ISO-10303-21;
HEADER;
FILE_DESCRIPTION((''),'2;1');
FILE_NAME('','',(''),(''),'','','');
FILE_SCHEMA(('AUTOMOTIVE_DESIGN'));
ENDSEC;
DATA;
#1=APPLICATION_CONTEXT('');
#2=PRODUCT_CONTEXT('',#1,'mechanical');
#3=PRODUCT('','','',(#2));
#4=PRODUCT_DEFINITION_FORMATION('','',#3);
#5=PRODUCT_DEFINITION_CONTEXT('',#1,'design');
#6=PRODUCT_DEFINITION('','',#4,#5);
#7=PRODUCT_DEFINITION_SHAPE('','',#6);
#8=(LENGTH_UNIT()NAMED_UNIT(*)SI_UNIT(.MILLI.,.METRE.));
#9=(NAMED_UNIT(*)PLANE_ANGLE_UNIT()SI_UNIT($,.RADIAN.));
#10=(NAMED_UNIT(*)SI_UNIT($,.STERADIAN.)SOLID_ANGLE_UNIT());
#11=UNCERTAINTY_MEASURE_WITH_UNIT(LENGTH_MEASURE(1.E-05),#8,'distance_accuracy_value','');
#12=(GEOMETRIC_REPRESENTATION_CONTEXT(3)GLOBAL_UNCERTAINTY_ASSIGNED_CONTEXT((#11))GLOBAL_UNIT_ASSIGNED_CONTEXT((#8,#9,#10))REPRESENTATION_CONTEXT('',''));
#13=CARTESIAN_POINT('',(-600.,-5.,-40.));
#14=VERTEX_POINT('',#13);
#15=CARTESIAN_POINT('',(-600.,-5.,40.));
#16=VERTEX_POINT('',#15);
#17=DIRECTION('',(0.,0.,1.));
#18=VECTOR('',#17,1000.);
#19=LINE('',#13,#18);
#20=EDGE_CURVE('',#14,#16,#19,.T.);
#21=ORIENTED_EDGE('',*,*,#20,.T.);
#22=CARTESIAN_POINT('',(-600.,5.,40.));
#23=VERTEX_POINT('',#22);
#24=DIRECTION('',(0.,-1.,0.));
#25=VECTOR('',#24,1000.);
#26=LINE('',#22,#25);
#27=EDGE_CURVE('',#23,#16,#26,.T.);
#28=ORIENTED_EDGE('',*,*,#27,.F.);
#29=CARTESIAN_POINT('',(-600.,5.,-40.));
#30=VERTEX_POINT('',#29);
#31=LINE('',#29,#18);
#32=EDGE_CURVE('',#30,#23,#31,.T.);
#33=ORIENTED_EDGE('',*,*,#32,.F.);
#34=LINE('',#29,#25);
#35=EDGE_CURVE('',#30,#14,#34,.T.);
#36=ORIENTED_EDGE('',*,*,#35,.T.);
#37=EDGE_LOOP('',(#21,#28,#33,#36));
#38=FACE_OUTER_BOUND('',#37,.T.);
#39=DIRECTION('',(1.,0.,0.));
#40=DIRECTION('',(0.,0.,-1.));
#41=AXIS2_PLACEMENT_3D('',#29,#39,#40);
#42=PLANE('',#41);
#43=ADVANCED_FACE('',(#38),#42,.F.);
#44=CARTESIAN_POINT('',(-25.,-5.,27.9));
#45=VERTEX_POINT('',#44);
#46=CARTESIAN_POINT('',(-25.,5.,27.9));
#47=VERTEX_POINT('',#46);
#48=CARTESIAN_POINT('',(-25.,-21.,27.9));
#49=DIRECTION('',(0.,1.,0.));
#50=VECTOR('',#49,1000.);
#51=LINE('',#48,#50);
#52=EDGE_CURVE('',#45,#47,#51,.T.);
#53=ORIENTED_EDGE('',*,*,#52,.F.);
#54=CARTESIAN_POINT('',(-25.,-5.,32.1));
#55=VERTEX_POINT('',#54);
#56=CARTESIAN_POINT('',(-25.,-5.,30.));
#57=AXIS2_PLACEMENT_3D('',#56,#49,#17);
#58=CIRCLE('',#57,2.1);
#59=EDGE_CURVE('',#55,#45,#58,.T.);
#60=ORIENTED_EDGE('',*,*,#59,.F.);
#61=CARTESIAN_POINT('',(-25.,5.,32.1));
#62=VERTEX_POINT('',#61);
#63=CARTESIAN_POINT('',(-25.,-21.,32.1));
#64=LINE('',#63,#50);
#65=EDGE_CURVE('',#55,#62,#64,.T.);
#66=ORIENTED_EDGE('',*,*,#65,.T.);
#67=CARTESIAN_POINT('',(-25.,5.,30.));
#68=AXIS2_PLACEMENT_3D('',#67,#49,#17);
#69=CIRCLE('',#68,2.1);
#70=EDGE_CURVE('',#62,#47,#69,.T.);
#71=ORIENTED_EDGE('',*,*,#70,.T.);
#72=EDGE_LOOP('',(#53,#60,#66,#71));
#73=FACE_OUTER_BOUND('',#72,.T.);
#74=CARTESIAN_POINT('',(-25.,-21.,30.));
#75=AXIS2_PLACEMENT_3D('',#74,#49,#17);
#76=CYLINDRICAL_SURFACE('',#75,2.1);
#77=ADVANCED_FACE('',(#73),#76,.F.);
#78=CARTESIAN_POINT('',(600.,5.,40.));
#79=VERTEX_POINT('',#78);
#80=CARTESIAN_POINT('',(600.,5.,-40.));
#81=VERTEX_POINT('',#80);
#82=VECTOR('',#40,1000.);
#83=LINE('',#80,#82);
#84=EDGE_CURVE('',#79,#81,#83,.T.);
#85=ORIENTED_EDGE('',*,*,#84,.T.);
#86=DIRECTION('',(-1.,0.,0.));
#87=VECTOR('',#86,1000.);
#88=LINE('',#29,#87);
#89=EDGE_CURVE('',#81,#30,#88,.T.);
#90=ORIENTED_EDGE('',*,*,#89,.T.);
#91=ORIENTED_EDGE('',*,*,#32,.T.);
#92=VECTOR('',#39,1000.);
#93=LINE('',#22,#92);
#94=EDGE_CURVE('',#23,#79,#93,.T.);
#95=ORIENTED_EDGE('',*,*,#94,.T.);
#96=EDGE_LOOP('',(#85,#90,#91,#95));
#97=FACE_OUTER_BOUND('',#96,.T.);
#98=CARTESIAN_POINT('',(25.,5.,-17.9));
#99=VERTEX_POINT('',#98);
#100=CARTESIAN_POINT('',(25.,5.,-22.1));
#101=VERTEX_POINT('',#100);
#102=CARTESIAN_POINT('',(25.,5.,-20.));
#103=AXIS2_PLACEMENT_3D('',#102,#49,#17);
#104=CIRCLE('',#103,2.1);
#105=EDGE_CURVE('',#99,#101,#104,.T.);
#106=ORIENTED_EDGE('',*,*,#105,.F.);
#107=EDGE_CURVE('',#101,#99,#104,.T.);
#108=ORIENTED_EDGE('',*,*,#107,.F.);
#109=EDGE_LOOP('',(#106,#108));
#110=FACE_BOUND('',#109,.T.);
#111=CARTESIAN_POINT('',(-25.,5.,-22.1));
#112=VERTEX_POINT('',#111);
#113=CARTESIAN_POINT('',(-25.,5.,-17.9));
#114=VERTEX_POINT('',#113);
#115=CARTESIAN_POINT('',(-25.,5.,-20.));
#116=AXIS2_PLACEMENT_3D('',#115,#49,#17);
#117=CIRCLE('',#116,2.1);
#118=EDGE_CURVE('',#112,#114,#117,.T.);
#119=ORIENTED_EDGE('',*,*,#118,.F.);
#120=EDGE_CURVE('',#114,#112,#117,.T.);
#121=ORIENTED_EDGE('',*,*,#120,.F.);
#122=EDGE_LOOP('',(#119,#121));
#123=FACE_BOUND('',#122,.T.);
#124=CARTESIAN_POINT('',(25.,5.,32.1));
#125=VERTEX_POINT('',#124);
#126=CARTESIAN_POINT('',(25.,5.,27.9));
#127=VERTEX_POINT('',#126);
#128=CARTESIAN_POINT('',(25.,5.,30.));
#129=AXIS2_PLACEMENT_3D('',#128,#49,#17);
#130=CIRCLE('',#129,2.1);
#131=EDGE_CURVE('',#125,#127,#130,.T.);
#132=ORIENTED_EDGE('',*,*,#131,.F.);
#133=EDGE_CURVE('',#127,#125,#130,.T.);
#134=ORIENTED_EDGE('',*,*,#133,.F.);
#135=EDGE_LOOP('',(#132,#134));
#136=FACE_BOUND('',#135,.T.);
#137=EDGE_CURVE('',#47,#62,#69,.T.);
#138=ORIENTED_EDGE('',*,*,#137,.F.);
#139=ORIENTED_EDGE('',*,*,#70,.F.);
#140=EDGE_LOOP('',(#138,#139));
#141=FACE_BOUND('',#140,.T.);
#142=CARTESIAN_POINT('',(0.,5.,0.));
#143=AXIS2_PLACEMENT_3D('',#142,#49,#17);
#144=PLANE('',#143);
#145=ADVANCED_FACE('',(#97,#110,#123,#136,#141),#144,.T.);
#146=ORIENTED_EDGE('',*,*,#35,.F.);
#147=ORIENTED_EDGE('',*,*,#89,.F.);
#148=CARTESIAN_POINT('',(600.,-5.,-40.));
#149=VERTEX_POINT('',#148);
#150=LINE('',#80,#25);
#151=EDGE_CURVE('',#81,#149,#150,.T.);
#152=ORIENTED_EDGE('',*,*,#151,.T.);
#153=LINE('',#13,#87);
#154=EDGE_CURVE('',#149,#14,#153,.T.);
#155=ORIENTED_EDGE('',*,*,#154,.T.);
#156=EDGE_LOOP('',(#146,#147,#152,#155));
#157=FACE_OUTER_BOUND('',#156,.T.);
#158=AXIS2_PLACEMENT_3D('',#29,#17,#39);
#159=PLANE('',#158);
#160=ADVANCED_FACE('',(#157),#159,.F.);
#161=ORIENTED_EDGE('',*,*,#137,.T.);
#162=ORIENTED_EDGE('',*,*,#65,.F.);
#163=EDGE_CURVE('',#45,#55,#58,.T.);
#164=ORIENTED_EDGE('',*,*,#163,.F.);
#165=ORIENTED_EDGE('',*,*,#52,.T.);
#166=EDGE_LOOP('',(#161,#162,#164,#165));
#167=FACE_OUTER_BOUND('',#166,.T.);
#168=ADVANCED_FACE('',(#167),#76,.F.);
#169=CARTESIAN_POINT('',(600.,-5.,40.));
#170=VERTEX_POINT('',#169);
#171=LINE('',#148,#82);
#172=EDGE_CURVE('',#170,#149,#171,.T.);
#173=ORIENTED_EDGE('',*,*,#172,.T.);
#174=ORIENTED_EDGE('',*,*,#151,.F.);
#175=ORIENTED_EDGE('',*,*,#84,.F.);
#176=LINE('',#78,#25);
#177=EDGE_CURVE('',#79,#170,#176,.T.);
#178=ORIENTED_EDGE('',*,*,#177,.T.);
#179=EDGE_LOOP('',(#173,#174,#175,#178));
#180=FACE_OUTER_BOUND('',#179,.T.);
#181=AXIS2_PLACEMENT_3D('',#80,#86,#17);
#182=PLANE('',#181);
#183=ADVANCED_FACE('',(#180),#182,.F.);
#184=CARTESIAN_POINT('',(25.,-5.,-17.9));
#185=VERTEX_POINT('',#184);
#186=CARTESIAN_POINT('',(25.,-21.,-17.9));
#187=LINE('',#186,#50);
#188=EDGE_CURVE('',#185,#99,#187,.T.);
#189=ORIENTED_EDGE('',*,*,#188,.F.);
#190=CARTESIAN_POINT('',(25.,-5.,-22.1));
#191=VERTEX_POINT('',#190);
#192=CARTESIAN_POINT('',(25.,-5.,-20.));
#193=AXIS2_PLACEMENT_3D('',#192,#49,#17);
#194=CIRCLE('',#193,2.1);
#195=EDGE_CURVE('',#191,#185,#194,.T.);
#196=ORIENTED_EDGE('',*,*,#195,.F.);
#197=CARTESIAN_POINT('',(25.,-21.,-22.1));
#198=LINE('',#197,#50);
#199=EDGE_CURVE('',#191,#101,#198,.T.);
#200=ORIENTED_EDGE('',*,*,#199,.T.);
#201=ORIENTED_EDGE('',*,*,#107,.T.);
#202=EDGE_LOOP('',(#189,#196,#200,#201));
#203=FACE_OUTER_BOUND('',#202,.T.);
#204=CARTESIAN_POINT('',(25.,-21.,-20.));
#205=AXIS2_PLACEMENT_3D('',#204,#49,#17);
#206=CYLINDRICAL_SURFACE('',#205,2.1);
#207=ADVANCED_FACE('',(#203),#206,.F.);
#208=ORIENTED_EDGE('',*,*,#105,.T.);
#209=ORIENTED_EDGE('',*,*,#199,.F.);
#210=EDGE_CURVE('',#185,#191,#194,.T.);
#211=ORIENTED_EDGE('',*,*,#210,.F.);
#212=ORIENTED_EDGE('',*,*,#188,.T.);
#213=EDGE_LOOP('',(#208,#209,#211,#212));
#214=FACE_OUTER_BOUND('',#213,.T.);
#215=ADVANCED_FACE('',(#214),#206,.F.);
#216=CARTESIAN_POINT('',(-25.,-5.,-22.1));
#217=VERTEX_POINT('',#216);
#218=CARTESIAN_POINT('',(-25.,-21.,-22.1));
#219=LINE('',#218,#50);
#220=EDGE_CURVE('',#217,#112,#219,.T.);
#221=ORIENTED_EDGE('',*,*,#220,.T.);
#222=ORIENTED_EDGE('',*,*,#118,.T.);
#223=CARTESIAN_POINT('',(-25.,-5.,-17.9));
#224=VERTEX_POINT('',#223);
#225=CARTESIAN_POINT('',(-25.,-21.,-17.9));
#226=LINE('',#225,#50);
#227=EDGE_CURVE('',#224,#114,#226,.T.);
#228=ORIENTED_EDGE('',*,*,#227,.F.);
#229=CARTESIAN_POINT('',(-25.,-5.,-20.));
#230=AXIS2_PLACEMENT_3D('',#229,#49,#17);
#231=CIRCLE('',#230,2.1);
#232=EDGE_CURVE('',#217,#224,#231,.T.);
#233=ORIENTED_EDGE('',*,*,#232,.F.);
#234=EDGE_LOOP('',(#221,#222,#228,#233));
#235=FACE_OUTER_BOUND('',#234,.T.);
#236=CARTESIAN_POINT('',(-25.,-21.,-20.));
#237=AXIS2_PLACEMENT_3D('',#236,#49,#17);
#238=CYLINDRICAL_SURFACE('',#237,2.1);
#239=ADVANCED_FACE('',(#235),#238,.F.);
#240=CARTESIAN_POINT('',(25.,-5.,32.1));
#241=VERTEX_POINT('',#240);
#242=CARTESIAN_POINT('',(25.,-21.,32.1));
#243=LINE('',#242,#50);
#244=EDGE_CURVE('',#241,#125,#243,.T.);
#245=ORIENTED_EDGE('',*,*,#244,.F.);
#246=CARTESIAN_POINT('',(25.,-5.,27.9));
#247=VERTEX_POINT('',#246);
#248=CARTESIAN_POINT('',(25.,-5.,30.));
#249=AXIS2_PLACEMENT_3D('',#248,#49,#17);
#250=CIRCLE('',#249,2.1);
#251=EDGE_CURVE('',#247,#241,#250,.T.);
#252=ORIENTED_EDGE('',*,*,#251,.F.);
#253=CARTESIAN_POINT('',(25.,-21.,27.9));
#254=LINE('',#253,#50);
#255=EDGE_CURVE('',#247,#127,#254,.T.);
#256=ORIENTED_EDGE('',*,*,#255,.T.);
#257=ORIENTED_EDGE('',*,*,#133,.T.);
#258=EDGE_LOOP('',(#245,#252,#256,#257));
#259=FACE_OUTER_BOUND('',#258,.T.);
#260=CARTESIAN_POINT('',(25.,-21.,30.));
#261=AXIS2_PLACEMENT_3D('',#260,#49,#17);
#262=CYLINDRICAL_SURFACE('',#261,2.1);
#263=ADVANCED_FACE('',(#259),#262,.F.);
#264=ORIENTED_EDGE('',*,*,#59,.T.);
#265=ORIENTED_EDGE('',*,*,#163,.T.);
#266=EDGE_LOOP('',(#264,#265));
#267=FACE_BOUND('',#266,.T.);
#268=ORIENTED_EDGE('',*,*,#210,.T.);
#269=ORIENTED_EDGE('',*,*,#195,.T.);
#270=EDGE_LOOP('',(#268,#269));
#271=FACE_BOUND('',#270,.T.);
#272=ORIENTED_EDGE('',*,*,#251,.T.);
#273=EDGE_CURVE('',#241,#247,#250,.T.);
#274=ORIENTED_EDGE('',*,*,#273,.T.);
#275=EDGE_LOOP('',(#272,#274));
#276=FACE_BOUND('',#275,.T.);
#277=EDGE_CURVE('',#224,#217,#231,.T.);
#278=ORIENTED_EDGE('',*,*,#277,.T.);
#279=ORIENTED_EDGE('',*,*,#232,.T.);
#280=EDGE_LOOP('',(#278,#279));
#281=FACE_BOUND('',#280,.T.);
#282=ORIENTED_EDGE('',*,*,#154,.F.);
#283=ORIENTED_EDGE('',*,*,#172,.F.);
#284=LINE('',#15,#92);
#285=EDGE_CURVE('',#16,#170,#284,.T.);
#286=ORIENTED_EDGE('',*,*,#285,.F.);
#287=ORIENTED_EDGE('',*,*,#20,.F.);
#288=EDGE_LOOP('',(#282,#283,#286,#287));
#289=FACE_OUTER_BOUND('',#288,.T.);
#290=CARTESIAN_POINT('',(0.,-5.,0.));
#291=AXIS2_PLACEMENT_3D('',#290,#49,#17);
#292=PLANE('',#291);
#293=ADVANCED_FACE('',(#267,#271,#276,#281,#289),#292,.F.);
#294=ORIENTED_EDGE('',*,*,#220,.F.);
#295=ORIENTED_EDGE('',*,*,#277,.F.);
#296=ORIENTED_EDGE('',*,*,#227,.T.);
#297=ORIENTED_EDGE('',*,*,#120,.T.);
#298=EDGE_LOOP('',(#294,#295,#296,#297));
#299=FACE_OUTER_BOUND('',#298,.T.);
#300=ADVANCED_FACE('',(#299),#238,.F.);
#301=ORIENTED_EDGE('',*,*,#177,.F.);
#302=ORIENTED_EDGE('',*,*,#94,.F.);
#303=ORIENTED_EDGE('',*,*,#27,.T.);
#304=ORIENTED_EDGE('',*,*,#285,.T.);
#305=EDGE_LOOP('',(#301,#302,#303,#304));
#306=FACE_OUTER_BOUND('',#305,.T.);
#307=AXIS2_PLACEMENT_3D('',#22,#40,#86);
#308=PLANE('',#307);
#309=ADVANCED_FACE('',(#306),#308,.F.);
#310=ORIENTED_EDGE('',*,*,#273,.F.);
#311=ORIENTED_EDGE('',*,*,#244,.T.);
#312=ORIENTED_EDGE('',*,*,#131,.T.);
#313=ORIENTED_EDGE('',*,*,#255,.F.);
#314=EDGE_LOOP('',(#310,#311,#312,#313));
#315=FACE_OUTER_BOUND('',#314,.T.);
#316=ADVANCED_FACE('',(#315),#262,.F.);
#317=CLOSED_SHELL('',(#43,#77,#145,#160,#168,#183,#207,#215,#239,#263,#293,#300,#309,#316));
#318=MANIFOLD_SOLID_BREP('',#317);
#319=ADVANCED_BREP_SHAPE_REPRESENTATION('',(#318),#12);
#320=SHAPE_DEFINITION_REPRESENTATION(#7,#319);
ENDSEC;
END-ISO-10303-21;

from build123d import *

# Parameters (mm, degrees)
SKETCH_2_W          = 1200
SKETCH_2_H          = 80
EXTRUDE_1_DEPTH     = 5
SKETCH_4_R          = 2.1
CUT_EXTRUDE_1_DEPTH = 26


with BuildPart() as part:
    # 草图2 → 凸台-拉伸1 (new, symmetric)
    with BuildSketch(Plane(origin=(0, 0, 0), x_dir=(1, 0, 0), z_dir=(0, 1, 0))):
        Rectangle(SKETCH_2_W, SKETCH_2_H)
    extrude(amount=EXTRUDE_1_DEPTH, both=True)

    # 草图4 → 切除-拉伸1 (cut)
    with BuildSketch(Plane(origin=(0, 5, 0), x_dir=(1, 0, 0), z_dir=(0, 1, 0))):
        with Locations(Location((-25, 20, 0), (0, 0, 270))):
            Circle(SKETCH_4_R)
        with Locations(Location((25, 20, 0), (0, 0, 270))):
            Circle(SKETCH_4_R)
        with Locations(Location((25, -30, 0), (0, 0, 270))):
            Circle(SKETCH_4_R)
        with Locations(Location((-25, -30, 0), (0, 0, 270))):
            Circle(SKETCH_4_R)
    extrude(amount=-CUT_EXTRUDE_1_DEPTH, mode=Mode.SUBTRACT)


solid = part.part
